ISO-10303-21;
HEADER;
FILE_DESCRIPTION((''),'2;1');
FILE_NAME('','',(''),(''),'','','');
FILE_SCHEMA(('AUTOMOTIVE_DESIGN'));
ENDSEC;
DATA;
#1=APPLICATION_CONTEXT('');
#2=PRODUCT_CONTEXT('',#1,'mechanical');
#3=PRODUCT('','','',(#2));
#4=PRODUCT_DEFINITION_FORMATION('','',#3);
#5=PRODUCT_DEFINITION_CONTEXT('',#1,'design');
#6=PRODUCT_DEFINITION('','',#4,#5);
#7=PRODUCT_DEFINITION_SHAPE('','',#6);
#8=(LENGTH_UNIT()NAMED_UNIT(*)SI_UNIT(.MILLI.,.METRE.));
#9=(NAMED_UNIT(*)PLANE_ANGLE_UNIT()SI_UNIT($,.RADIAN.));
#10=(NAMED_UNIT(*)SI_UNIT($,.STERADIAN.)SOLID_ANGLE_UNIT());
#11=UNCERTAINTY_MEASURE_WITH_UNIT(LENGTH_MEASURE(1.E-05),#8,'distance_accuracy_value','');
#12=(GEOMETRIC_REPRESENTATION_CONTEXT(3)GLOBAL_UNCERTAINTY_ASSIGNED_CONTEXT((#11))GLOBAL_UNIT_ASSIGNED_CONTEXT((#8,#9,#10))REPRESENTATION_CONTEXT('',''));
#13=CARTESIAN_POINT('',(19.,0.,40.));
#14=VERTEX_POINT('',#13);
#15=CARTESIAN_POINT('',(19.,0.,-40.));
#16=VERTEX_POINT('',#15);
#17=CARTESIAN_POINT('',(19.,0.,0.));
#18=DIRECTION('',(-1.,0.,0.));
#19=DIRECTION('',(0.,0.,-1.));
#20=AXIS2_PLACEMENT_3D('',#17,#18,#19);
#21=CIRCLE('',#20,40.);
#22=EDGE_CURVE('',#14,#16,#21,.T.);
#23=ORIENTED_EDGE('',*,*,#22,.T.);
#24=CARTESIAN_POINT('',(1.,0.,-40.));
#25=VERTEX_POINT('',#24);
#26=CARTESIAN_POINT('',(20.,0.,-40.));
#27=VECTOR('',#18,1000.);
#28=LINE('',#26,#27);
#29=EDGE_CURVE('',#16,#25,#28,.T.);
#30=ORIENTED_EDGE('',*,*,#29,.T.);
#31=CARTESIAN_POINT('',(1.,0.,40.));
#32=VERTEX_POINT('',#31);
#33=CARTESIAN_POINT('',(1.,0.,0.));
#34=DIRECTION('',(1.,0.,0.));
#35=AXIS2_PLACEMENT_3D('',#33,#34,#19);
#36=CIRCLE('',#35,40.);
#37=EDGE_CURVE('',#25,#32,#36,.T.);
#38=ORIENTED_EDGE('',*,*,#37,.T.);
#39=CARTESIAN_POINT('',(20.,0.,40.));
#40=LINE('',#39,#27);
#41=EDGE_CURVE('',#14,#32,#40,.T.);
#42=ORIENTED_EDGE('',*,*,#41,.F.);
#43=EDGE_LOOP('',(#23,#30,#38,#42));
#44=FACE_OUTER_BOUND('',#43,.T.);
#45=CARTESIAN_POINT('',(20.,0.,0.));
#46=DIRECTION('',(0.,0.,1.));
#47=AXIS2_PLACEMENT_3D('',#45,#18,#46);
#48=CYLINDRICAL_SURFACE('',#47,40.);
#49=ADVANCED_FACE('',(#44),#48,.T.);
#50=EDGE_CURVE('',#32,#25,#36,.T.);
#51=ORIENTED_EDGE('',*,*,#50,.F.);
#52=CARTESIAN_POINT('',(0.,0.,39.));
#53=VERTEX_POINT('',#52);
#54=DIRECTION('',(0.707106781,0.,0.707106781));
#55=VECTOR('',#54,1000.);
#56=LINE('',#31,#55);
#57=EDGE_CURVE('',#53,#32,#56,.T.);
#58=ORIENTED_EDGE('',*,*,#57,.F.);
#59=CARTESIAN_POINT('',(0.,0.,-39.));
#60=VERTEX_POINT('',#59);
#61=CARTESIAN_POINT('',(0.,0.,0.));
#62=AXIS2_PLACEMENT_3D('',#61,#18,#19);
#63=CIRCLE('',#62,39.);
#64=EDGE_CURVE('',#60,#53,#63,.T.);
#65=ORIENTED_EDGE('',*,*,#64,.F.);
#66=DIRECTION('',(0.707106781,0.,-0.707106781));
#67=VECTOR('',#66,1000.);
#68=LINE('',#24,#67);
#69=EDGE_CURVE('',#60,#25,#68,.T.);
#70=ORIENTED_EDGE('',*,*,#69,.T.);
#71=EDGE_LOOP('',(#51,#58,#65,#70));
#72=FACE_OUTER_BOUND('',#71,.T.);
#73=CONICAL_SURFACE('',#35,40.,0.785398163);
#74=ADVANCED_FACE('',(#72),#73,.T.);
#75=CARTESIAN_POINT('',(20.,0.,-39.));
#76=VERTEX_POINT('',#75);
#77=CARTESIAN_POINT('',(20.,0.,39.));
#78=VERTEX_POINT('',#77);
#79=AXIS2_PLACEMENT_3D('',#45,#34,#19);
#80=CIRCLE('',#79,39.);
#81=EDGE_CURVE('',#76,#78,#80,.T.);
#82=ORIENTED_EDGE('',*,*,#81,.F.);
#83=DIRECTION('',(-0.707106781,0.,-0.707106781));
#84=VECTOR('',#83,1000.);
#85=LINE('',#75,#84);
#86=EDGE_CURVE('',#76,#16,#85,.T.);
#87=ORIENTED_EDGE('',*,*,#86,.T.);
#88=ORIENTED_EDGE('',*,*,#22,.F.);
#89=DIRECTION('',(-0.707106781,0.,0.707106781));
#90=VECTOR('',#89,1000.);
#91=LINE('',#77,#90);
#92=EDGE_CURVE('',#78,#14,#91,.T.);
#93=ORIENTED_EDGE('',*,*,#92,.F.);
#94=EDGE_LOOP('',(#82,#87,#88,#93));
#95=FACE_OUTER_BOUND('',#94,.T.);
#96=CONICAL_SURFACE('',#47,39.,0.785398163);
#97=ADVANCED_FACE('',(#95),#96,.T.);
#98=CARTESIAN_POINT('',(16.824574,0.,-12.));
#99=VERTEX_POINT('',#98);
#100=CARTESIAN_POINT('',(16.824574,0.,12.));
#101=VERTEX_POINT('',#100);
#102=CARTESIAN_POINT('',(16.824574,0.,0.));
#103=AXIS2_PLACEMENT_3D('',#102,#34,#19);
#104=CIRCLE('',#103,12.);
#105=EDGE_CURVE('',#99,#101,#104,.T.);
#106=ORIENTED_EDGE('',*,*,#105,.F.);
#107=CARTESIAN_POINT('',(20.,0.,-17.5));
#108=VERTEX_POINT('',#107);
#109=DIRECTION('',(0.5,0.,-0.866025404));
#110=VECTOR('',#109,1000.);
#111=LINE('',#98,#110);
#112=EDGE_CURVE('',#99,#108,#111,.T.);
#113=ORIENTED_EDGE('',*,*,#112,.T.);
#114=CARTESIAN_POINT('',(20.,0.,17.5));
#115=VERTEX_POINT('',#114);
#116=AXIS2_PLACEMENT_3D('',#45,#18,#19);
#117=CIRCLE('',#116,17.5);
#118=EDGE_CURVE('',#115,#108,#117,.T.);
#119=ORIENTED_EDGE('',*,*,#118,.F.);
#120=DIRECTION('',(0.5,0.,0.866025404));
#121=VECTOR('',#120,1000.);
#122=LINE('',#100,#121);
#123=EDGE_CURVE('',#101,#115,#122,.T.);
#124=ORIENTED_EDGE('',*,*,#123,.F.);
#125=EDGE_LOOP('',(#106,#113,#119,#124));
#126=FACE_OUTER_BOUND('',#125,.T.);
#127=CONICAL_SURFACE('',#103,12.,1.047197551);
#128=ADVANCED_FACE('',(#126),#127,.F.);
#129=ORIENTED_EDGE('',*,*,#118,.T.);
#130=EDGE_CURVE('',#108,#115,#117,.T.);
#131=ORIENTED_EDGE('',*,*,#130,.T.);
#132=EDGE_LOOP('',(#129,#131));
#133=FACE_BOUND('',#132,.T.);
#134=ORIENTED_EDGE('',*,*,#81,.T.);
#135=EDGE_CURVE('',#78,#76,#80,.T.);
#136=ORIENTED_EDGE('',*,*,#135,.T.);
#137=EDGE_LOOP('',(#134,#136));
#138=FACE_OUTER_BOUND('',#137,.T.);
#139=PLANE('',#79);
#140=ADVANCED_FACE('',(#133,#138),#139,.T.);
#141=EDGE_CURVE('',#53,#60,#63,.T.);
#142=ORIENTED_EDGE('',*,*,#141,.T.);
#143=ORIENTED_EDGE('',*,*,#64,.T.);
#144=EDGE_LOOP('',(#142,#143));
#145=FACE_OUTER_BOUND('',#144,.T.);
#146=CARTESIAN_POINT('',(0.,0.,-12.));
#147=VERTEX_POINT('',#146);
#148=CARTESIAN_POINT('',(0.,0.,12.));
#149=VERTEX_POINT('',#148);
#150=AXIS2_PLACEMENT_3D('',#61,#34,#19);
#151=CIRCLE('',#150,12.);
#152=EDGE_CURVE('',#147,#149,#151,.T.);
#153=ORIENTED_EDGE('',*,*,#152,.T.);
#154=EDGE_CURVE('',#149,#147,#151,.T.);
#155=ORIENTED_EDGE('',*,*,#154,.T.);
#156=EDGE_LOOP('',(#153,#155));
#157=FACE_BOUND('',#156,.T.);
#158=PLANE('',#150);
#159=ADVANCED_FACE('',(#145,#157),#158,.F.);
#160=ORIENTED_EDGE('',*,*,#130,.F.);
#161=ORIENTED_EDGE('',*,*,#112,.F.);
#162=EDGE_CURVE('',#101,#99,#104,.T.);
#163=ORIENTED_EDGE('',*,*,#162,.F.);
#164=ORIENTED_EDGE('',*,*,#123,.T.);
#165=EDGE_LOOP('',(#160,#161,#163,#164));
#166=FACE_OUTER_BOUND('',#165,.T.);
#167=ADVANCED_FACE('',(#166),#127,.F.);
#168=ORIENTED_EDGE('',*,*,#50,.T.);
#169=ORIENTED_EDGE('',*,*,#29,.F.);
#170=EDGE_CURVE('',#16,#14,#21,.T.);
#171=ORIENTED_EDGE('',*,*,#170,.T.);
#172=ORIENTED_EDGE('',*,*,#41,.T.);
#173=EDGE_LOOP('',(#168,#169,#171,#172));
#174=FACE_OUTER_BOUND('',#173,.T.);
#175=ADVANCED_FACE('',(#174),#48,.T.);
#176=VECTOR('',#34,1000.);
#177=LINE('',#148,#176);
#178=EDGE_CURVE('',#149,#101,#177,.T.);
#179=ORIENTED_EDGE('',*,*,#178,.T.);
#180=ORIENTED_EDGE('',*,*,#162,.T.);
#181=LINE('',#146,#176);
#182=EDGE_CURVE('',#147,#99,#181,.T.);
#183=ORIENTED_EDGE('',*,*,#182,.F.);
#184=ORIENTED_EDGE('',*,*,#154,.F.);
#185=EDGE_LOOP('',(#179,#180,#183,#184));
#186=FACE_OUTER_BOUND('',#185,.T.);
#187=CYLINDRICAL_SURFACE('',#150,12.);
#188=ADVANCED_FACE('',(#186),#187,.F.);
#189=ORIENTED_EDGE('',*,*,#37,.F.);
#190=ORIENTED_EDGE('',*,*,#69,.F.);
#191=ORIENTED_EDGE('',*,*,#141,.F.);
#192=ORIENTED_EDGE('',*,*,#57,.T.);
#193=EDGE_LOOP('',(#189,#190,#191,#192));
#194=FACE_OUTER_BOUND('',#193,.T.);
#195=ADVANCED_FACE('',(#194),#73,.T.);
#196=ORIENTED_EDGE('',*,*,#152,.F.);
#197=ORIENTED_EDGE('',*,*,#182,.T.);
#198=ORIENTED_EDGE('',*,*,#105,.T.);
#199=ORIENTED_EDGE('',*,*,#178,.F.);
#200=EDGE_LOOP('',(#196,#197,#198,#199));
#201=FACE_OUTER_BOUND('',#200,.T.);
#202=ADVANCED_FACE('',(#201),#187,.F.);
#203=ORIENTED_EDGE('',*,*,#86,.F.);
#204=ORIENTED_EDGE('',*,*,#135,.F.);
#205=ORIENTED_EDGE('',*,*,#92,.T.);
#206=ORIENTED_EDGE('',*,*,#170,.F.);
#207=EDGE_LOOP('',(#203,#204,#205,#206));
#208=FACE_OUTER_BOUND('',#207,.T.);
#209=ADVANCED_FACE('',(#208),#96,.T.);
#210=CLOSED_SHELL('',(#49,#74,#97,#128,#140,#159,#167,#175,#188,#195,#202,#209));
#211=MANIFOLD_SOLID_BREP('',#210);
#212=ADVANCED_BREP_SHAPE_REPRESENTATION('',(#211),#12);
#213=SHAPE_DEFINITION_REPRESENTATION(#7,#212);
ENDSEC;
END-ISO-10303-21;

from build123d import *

# Parameters (mm, degrees)
SKETCH1_R          = 40
EXTRUDE1_DEPTH     = 20
SKETCH2_R          = 12
CUT_EXTRUDE1_DEPTH = 61
CHAMFER1_SIZE      = 1
CHAMFER2_SIZE      = 5.5
CHAMFER2_SIZE2     = 3.175426481


with BuildPart() as part:
    # Sketch1 → Extrude1 (new body)
    with BuildSketch(Plane(origin=(0, 0, 0), x_dir=(0, 0, -1), z_dir=(1, 0, 0))):
        Circle(SKETCH1_R)
    extrude(amount=EXTRUDE1_DEPTH)

    # Sketch2 → Cut-Extrude1 (cut, through all)
    with BuildSketch(Plane(origin=(20, 0, 0), x_dir=(0, 0, -1), z_dir=(1, 0, 0))):
        Circle(SKETCH2_R)
    extrude(amount=-CUT_EXTRUDE1_DEPTH, mode=Mode.SUBTRACT)

    # Chamfer1
    chamfer1_edges = [part.edges().sort_by_distance(p)[0] for p in [
        (0, 0, 40),
        (20, 0, 40),
    ]]
    chamfer(chamfer1_edges, length=CHAMFER1_SIZE)

    # Chamfer2
    chamfer2_edges = [part.edges().sort_by_distance(p)[0] for p in [
        (20, 0, 12),
    ]]
    chamfer2_side = [part.faces().sort_by_distance(p)[0] for p in [
        (20, 0, 37.896913421),
    ]]
    chamfer(chamfer2_edges, length=CHAMFER2_SIZE, length2=CHAMFER2_SIZE2, reference=chamfer2_side[0])


solid = part.part
